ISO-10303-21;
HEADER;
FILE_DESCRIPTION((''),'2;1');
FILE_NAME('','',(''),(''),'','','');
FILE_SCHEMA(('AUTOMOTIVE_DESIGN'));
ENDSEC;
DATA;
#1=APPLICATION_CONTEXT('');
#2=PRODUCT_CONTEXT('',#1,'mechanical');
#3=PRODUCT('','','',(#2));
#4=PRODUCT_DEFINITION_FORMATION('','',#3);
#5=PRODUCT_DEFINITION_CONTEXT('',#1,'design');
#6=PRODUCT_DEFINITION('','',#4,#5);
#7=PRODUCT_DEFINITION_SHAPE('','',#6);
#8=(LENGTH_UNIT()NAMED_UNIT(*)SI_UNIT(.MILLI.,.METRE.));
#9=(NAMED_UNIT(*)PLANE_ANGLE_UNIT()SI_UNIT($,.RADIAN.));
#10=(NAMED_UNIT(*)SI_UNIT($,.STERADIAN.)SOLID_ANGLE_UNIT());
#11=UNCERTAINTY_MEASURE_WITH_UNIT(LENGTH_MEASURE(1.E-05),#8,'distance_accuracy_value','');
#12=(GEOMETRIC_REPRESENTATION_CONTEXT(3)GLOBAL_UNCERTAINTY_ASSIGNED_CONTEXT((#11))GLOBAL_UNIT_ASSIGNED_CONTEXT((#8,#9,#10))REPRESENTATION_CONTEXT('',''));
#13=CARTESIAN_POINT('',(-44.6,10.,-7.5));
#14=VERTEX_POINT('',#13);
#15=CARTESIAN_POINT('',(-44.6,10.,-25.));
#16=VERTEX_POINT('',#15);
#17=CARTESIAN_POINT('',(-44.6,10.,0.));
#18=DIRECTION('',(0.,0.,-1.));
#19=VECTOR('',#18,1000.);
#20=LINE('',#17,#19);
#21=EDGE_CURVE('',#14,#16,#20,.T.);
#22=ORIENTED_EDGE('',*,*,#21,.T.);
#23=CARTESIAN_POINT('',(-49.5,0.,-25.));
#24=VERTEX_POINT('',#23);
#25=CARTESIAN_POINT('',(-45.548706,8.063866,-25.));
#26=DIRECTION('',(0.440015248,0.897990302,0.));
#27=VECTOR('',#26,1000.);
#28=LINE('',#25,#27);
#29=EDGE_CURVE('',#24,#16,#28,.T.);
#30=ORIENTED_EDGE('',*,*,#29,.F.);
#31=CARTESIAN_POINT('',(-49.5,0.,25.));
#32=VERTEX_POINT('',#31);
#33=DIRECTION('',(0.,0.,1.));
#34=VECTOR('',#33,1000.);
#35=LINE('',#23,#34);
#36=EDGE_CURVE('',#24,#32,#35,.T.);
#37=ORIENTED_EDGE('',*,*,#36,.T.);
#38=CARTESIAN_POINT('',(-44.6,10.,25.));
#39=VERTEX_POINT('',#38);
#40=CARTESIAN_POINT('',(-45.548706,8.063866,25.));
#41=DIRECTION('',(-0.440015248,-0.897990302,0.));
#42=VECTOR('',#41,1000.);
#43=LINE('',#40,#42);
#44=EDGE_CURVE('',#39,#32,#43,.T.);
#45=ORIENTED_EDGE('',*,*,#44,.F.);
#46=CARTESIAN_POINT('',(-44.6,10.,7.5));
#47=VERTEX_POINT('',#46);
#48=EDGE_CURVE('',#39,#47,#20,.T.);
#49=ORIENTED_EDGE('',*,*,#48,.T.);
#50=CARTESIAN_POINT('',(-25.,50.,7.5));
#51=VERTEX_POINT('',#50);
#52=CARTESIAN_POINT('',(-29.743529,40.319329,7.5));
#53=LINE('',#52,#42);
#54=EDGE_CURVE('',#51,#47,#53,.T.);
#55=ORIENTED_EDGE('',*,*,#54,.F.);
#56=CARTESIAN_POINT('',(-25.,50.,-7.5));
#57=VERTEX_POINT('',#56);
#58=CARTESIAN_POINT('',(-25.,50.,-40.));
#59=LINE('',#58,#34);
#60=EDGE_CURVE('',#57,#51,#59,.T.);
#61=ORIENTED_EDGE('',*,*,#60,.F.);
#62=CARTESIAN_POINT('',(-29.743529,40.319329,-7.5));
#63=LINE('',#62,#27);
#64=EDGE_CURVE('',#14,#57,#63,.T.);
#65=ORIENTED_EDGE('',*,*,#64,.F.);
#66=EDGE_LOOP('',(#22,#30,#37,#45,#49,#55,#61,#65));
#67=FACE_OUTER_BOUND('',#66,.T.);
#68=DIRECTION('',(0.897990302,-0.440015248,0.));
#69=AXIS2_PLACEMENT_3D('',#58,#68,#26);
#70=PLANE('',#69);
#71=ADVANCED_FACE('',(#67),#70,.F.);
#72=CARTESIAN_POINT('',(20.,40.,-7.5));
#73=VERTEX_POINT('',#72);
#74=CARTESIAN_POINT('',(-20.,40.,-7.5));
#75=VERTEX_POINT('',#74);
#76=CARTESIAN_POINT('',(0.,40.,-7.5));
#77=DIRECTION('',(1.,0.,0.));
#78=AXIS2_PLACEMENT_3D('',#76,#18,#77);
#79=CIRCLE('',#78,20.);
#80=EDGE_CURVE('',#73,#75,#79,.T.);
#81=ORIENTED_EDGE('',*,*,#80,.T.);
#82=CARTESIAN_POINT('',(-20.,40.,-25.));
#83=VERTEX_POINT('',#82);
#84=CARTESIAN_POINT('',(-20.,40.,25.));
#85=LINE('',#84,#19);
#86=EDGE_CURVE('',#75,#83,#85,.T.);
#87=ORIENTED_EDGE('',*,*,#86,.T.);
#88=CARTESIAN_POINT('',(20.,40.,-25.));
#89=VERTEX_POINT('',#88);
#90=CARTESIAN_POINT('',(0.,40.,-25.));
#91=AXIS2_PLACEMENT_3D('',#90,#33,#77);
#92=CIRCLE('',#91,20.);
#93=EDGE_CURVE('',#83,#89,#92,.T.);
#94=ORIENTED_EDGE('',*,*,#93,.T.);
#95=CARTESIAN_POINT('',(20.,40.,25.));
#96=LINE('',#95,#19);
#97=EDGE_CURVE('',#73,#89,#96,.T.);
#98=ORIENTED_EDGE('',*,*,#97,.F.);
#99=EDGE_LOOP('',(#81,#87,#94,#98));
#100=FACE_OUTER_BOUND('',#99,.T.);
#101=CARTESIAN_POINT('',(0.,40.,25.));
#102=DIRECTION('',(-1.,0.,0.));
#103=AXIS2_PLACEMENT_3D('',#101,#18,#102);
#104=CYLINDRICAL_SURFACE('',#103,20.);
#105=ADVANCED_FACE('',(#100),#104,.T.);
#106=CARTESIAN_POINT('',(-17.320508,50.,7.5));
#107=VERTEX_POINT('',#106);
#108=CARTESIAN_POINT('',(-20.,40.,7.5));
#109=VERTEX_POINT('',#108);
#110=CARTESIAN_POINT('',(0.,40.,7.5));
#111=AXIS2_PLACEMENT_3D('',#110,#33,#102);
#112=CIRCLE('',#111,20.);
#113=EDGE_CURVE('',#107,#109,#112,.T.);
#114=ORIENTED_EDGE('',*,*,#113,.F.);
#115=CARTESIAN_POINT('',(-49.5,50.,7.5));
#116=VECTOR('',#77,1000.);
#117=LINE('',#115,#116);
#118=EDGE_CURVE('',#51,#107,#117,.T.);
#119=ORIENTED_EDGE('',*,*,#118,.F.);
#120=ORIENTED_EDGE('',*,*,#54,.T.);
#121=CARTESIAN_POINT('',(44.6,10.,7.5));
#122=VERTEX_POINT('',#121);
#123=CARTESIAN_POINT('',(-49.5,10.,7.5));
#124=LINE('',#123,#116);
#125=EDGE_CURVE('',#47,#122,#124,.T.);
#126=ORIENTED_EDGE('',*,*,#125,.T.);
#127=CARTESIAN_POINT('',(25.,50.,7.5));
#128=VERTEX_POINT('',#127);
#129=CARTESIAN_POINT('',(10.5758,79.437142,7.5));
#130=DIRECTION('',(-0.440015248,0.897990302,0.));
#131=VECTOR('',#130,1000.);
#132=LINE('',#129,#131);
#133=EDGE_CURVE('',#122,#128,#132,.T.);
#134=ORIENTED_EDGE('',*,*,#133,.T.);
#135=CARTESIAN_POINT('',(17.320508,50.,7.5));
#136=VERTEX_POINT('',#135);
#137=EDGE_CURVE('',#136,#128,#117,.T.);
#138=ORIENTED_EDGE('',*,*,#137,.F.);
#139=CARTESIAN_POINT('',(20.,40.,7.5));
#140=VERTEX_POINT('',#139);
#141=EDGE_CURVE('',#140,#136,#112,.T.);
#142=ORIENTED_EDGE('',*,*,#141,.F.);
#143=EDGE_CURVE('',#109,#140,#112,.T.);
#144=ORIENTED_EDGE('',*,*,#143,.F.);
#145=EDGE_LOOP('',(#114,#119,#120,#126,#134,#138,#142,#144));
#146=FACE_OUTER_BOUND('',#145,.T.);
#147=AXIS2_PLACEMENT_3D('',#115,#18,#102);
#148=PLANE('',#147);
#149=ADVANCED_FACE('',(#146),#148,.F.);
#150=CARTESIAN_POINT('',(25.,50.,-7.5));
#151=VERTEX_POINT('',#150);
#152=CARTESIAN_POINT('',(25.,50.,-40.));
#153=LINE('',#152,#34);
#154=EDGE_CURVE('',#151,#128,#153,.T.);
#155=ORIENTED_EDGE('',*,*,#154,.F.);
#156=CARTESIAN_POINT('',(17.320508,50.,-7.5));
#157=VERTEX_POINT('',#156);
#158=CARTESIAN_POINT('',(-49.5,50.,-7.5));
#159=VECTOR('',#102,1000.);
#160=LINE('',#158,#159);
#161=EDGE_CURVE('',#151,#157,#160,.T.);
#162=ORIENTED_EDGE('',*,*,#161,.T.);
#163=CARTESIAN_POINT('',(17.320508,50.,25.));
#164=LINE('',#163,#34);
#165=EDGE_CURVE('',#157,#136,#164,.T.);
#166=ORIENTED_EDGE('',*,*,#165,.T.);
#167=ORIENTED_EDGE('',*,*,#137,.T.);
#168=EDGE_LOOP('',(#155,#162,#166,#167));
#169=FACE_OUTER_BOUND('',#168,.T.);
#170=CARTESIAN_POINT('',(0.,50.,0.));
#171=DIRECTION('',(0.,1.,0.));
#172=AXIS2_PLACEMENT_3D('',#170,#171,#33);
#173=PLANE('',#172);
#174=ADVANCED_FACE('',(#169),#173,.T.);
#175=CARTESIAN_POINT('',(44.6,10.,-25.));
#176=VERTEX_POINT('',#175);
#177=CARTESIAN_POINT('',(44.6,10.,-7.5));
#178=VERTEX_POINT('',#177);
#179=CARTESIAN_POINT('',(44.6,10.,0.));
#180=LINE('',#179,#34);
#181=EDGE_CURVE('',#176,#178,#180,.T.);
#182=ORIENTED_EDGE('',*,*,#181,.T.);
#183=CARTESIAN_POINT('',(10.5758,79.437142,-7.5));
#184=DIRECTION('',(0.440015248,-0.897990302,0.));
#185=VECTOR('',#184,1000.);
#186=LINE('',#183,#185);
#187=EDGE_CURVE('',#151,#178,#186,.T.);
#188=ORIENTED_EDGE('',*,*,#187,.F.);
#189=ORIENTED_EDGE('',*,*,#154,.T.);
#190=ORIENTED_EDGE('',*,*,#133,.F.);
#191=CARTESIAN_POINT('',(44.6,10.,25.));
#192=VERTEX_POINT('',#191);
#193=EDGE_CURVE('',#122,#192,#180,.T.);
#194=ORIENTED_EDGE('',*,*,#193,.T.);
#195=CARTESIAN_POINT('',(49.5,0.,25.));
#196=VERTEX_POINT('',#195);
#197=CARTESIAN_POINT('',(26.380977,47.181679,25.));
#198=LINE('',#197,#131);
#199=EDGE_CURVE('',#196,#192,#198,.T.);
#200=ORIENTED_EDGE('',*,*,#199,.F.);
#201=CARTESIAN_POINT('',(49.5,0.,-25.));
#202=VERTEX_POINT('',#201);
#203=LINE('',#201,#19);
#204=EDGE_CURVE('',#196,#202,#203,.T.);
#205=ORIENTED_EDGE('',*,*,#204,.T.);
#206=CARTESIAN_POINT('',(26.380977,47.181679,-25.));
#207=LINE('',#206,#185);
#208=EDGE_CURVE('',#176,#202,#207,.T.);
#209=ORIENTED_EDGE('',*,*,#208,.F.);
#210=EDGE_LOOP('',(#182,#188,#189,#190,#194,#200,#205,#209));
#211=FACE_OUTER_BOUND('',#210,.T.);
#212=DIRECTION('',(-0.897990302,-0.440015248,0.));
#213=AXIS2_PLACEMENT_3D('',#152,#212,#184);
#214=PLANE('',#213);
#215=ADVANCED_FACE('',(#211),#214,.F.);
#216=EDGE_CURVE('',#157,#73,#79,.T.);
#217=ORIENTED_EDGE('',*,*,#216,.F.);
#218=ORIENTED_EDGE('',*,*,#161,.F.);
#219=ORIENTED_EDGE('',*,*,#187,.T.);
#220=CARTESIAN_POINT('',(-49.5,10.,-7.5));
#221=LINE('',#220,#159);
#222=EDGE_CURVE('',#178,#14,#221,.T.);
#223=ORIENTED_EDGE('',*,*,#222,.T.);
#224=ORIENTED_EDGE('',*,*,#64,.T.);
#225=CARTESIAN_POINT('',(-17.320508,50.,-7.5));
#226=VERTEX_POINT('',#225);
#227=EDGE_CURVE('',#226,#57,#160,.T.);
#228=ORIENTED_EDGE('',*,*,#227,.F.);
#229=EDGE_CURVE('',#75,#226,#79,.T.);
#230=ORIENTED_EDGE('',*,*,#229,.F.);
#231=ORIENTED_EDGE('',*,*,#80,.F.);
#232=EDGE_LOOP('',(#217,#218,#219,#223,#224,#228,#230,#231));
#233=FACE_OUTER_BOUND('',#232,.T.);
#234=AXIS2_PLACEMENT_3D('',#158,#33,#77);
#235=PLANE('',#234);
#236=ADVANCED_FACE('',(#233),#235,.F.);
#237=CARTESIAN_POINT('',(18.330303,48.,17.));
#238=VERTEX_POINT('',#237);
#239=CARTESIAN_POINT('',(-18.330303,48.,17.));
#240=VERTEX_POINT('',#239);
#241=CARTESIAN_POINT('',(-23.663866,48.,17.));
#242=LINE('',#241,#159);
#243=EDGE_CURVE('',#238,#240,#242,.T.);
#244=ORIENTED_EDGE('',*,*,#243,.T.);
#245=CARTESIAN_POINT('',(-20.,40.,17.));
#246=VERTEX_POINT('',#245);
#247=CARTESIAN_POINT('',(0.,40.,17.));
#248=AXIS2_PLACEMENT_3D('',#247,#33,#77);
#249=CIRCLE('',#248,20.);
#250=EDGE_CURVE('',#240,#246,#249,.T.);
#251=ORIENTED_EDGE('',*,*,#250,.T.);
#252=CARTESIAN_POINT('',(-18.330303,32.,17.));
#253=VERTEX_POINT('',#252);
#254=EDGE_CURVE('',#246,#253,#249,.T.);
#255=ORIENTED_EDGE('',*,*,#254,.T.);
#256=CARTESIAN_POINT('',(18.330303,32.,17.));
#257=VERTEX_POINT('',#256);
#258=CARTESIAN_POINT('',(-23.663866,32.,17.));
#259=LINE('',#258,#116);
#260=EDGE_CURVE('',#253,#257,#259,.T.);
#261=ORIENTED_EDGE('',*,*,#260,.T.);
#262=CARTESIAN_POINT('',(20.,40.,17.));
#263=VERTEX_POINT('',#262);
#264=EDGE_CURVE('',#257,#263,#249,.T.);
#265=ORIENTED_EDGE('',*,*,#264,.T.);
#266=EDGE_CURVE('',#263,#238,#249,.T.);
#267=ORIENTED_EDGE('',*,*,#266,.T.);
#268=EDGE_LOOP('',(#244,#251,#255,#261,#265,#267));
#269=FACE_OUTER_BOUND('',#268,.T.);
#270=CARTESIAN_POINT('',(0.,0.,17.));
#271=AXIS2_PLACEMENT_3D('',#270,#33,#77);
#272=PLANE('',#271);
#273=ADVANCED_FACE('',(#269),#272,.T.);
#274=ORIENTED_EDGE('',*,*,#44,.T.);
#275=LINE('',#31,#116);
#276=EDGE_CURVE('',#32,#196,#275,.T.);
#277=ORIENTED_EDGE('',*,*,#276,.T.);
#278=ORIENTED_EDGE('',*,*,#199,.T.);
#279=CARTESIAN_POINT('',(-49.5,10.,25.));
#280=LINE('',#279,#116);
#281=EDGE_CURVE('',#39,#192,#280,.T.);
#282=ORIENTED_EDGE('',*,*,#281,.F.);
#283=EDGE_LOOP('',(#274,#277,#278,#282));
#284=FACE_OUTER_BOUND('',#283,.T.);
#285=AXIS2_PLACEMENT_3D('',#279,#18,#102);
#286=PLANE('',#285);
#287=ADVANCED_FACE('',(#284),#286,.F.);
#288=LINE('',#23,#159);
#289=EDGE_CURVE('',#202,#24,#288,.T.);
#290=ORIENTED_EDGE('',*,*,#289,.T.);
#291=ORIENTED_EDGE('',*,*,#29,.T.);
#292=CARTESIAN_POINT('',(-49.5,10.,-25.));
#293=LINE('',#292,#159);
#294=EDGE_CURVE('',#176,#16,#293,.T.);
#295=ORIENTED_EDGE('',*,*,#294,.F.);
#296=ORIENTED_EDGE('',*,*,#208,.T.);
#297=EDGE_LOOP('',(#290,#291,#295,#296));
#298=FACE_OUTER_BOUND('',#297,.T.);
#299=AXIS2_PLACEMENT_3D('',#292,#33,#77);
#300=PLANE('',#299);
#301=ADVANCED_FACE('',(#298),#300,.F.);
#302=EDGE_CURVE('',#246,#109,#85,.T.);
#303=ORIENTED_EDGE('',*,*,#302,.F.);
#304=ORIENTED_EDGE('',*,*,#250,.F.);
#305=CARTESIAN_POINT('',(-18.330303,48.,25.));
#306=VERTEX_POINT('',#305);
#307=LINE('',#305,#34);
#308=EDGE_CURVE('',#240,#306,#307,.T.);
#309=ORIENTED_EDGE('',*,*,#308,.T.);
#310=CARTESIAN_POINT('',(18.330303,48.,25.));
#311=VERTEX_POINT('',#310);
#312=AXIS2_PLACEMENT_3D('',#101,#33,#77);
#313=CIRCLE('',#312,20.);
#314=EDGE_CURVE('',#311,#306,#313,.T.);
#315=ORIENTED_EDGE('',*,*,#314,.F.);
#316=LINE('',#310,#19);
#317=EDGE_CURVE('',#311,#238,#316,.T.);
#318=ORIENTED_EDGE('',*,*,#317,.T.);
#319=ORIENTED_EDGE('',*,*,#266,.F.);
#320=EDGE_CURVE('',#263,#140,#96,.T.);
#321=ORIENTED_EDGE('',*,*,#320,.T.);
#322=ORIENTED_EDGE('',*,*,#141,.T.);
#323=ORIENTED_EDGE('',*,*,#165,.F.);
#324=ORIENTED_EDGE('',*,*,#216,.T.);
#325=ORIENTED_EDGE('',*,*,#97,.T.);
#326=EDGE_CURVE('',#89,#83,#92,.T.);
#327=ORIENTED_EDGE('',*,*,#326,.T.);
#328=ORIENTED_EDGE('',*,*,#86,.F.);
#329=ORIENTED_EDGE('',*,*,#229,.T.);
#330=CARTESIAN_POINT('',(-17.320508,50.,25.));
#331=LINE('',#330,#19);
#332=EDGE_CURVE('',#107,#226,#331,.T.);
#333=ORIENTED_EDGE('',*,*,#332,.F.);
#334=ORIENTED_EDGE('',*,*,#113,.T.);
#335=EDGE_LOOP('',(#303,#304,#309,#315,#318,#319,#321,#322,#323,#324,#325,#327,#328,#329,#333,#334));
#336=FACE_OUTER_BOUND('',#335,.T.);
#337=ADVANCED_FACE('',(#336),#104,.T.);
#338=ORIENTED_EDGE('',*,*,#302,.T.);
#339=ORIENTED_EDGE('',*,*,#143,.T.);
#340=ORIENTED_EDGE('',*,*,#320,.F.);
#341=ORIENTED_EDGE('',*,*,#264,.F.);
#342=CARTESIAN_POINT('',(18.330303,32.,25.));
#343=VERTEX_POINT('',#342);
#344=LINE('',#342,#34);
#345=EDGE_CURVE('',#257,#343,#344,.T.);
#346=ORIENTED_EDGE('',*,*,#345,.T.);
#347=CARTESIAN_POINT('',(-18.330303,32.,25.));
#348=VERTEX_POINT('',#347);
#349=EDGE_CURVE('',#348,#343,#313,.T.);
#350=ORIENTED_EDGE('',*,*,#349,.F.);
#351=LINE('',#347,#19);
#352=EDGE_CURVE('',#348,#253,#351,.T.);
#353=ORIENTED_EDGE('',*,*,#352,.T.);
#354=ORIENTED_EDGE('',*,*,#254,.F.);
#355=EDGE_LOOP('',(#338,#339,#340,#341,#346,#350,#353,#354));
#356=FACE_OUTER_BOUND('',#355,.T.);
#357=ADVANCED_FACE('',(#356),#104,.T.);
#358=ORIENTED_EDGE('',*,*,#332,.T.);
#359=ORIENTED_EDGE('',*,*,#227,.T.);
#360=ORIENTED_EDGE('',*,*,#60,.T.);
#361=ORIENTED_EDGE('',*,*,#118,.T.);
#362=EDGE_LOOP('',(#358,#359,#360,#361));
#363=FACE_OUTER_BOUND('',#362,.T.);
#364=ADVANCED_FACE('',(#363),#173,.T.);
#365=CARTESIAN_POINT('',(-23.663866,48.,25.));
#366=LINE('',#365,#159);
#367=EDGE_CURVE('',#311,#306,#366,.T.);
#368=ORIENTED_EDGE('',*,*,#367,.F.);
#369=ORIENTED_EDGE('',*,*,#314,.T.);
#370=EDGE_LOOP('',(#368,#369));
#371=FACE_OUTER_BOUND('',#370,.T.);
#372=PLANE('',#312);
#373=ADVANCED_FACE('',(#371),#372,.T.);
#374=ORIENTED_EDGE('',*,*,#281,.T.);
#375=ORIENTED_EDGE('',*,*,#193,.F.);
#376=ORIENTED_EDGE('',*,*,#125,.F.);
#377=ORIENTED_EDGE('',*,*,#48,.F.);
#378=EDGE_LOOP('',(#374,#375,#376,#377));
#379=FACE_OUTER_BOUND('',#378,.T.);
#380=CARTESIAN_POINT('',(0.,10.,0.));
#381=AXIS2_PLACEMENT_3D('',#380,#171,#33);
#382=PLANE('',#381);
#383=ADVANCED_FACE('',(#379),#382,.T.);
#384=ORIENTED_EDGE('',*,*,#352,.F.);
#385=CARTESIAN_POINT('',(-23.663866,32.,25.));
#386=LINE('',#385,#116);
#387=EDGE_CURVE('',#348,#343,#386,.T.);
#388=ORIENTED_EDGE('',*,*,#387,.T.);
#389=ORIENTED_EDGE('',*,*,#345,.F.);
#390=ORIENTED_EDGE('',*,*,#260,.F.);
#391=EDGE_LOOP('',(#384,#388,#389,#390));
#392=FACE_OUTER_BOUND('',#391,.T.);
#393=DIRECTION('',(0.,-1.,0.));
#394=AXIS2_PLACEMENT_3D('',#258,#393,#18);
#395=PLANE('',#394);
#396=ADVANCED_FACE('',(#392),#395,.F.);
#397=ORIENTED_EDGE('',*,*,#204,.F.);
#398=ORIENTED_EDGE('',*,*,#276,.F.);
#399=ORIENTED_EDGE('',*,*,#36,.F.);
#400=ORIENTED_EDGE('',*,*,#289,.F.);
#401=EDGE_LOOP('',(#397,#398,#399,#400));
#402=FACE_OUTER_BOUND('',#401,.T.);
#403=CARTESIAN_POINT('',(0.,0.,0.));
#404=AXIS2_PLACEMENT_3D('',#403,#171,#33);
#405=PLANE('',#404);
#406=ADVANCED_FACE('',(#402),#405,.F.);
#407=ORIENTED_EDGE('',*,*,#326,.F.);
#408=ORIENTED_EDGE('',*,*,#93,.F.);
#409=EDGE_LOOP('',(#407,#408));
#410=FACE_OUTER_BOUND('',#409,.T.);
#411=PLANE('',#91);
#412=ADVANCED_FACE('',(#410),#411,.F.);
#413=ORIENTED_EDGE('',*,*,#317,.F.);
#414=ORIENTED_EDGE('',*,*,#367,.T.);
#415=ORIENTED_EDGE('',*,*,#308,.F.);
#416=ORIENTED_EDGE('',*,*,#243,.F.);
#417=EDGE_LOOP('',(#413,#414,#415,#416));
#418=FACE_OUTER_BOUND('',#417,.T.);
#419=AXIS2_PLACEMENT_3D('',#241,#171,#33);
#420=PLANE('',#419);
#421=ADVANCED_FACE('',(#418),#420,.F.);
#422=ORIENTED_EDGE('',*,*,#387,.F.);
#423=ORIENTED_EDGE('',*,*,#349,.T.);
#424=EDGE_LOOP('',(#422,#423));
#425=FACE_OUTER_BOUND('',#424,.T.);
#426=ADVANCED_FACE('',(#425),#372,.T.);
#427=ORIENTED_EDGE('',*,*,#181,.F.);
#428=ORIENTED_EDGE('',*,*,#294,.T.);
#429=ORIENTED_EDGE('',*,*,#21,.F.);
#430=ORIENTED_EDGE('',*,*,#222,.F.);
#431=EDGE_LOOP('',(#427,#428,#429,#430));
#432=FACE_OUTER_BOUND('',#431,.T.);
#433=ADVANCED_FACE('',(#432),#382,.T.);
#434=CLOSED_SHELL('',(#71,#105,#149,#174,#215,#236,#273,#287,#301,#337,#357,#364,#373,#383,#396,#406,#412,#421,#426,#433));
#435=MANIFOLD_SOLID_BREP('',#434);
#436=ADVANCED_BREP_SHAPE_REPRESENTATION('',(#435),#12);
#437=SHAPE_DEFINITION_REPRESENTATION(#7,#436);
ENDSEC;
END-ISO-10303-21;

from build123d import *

# Parameters (mm, degrees)
BASE_PLATE_SKETCH_W     = 99
BASE_PLATE_SKETCH_H     = 50
BASE_PLATE_DEPTH        = 10
SUPPORT_BLOCK_SKETCH_W  = 99
SUPPORT_BLOCK_SKETCH_H  = 15
SUPPORT_BLOCK_DEPTH     = 40
SUPPORT_TAPER_CUT_DEPTH = 40
CYLINDER_BOSS_SKETCH_R  = 20
CYLINDER_BOSS_40_DEPTH  = 25
END_SLOT_SKETCH_W       = 47.327731092
END_SLOT_SKETCH_H       = 16
END_SLOT_16X8_DEPTH     = 8


with BuildPart() as part:
    # Base Plate Sketch → Base Plate (new body)
    with BuildSketch(Plane(origin=(0, 0, 0), x_dir=(1, 0, 0), z_dir=(0, 1, 0))):
        Rectangle(BASE_PLATE_SKETCH_W, BASE_PLATE_SKETCH_H)
    extrude(amount=BASE_PLATE_DEPTH)

    # Support Block Sketch → Support Block (add)
    with BuildSketch(Plane(origin=(0, 10, 0), x_dir=(1, 0, 0), z_dir=(0, 1, 0))):
        Rectangle(SUPPORT_BLOCK_SKETCH_W, SUPPORT_BLOCK_SKETCH_H)
    extrude(amount=SUPPORT_BLOCK_DEPTH)

    # Support Taper Sketch → Support Taper Cut (cut, symmetric)
    with BuildSketch(Plane.XY):
        Polygon((-25, 50), (-49.5, 0), (-49.5, 50), align=None)
        Polygon((25, 50), (49.5, 0), (49.5, 50), align=None)
    extrude(amount=SUPPORT_TAPER_CUT_DEPTH, both=True, mode=Mode.SUBTRACT)

    # Cylinder Boss Sketch → Cylinder Boss Ø40 (add, symmetric)
    with BuildSketch(Plane.XY):
        with Locations((0, 40)):
            Circle(CYLINDER_BOSS_SKETCH_R)
    extrude(amount=CYLINDER_BOSS_40_DEPTH, both=True)

    # End Slot Sketch → End Slot 16x8 (cut)
    with BuildSketch(Plane.XY.offset(25)):
        with Locations((0, 40)):
            Rectangle(END_SLOT_SKETCH_W, END_SLOT_SKETCH_H)
    extrude(amount=-END_SLOT_16X8_DEPTH, mode=Mode.SUBTRACT)


solid = part.part
